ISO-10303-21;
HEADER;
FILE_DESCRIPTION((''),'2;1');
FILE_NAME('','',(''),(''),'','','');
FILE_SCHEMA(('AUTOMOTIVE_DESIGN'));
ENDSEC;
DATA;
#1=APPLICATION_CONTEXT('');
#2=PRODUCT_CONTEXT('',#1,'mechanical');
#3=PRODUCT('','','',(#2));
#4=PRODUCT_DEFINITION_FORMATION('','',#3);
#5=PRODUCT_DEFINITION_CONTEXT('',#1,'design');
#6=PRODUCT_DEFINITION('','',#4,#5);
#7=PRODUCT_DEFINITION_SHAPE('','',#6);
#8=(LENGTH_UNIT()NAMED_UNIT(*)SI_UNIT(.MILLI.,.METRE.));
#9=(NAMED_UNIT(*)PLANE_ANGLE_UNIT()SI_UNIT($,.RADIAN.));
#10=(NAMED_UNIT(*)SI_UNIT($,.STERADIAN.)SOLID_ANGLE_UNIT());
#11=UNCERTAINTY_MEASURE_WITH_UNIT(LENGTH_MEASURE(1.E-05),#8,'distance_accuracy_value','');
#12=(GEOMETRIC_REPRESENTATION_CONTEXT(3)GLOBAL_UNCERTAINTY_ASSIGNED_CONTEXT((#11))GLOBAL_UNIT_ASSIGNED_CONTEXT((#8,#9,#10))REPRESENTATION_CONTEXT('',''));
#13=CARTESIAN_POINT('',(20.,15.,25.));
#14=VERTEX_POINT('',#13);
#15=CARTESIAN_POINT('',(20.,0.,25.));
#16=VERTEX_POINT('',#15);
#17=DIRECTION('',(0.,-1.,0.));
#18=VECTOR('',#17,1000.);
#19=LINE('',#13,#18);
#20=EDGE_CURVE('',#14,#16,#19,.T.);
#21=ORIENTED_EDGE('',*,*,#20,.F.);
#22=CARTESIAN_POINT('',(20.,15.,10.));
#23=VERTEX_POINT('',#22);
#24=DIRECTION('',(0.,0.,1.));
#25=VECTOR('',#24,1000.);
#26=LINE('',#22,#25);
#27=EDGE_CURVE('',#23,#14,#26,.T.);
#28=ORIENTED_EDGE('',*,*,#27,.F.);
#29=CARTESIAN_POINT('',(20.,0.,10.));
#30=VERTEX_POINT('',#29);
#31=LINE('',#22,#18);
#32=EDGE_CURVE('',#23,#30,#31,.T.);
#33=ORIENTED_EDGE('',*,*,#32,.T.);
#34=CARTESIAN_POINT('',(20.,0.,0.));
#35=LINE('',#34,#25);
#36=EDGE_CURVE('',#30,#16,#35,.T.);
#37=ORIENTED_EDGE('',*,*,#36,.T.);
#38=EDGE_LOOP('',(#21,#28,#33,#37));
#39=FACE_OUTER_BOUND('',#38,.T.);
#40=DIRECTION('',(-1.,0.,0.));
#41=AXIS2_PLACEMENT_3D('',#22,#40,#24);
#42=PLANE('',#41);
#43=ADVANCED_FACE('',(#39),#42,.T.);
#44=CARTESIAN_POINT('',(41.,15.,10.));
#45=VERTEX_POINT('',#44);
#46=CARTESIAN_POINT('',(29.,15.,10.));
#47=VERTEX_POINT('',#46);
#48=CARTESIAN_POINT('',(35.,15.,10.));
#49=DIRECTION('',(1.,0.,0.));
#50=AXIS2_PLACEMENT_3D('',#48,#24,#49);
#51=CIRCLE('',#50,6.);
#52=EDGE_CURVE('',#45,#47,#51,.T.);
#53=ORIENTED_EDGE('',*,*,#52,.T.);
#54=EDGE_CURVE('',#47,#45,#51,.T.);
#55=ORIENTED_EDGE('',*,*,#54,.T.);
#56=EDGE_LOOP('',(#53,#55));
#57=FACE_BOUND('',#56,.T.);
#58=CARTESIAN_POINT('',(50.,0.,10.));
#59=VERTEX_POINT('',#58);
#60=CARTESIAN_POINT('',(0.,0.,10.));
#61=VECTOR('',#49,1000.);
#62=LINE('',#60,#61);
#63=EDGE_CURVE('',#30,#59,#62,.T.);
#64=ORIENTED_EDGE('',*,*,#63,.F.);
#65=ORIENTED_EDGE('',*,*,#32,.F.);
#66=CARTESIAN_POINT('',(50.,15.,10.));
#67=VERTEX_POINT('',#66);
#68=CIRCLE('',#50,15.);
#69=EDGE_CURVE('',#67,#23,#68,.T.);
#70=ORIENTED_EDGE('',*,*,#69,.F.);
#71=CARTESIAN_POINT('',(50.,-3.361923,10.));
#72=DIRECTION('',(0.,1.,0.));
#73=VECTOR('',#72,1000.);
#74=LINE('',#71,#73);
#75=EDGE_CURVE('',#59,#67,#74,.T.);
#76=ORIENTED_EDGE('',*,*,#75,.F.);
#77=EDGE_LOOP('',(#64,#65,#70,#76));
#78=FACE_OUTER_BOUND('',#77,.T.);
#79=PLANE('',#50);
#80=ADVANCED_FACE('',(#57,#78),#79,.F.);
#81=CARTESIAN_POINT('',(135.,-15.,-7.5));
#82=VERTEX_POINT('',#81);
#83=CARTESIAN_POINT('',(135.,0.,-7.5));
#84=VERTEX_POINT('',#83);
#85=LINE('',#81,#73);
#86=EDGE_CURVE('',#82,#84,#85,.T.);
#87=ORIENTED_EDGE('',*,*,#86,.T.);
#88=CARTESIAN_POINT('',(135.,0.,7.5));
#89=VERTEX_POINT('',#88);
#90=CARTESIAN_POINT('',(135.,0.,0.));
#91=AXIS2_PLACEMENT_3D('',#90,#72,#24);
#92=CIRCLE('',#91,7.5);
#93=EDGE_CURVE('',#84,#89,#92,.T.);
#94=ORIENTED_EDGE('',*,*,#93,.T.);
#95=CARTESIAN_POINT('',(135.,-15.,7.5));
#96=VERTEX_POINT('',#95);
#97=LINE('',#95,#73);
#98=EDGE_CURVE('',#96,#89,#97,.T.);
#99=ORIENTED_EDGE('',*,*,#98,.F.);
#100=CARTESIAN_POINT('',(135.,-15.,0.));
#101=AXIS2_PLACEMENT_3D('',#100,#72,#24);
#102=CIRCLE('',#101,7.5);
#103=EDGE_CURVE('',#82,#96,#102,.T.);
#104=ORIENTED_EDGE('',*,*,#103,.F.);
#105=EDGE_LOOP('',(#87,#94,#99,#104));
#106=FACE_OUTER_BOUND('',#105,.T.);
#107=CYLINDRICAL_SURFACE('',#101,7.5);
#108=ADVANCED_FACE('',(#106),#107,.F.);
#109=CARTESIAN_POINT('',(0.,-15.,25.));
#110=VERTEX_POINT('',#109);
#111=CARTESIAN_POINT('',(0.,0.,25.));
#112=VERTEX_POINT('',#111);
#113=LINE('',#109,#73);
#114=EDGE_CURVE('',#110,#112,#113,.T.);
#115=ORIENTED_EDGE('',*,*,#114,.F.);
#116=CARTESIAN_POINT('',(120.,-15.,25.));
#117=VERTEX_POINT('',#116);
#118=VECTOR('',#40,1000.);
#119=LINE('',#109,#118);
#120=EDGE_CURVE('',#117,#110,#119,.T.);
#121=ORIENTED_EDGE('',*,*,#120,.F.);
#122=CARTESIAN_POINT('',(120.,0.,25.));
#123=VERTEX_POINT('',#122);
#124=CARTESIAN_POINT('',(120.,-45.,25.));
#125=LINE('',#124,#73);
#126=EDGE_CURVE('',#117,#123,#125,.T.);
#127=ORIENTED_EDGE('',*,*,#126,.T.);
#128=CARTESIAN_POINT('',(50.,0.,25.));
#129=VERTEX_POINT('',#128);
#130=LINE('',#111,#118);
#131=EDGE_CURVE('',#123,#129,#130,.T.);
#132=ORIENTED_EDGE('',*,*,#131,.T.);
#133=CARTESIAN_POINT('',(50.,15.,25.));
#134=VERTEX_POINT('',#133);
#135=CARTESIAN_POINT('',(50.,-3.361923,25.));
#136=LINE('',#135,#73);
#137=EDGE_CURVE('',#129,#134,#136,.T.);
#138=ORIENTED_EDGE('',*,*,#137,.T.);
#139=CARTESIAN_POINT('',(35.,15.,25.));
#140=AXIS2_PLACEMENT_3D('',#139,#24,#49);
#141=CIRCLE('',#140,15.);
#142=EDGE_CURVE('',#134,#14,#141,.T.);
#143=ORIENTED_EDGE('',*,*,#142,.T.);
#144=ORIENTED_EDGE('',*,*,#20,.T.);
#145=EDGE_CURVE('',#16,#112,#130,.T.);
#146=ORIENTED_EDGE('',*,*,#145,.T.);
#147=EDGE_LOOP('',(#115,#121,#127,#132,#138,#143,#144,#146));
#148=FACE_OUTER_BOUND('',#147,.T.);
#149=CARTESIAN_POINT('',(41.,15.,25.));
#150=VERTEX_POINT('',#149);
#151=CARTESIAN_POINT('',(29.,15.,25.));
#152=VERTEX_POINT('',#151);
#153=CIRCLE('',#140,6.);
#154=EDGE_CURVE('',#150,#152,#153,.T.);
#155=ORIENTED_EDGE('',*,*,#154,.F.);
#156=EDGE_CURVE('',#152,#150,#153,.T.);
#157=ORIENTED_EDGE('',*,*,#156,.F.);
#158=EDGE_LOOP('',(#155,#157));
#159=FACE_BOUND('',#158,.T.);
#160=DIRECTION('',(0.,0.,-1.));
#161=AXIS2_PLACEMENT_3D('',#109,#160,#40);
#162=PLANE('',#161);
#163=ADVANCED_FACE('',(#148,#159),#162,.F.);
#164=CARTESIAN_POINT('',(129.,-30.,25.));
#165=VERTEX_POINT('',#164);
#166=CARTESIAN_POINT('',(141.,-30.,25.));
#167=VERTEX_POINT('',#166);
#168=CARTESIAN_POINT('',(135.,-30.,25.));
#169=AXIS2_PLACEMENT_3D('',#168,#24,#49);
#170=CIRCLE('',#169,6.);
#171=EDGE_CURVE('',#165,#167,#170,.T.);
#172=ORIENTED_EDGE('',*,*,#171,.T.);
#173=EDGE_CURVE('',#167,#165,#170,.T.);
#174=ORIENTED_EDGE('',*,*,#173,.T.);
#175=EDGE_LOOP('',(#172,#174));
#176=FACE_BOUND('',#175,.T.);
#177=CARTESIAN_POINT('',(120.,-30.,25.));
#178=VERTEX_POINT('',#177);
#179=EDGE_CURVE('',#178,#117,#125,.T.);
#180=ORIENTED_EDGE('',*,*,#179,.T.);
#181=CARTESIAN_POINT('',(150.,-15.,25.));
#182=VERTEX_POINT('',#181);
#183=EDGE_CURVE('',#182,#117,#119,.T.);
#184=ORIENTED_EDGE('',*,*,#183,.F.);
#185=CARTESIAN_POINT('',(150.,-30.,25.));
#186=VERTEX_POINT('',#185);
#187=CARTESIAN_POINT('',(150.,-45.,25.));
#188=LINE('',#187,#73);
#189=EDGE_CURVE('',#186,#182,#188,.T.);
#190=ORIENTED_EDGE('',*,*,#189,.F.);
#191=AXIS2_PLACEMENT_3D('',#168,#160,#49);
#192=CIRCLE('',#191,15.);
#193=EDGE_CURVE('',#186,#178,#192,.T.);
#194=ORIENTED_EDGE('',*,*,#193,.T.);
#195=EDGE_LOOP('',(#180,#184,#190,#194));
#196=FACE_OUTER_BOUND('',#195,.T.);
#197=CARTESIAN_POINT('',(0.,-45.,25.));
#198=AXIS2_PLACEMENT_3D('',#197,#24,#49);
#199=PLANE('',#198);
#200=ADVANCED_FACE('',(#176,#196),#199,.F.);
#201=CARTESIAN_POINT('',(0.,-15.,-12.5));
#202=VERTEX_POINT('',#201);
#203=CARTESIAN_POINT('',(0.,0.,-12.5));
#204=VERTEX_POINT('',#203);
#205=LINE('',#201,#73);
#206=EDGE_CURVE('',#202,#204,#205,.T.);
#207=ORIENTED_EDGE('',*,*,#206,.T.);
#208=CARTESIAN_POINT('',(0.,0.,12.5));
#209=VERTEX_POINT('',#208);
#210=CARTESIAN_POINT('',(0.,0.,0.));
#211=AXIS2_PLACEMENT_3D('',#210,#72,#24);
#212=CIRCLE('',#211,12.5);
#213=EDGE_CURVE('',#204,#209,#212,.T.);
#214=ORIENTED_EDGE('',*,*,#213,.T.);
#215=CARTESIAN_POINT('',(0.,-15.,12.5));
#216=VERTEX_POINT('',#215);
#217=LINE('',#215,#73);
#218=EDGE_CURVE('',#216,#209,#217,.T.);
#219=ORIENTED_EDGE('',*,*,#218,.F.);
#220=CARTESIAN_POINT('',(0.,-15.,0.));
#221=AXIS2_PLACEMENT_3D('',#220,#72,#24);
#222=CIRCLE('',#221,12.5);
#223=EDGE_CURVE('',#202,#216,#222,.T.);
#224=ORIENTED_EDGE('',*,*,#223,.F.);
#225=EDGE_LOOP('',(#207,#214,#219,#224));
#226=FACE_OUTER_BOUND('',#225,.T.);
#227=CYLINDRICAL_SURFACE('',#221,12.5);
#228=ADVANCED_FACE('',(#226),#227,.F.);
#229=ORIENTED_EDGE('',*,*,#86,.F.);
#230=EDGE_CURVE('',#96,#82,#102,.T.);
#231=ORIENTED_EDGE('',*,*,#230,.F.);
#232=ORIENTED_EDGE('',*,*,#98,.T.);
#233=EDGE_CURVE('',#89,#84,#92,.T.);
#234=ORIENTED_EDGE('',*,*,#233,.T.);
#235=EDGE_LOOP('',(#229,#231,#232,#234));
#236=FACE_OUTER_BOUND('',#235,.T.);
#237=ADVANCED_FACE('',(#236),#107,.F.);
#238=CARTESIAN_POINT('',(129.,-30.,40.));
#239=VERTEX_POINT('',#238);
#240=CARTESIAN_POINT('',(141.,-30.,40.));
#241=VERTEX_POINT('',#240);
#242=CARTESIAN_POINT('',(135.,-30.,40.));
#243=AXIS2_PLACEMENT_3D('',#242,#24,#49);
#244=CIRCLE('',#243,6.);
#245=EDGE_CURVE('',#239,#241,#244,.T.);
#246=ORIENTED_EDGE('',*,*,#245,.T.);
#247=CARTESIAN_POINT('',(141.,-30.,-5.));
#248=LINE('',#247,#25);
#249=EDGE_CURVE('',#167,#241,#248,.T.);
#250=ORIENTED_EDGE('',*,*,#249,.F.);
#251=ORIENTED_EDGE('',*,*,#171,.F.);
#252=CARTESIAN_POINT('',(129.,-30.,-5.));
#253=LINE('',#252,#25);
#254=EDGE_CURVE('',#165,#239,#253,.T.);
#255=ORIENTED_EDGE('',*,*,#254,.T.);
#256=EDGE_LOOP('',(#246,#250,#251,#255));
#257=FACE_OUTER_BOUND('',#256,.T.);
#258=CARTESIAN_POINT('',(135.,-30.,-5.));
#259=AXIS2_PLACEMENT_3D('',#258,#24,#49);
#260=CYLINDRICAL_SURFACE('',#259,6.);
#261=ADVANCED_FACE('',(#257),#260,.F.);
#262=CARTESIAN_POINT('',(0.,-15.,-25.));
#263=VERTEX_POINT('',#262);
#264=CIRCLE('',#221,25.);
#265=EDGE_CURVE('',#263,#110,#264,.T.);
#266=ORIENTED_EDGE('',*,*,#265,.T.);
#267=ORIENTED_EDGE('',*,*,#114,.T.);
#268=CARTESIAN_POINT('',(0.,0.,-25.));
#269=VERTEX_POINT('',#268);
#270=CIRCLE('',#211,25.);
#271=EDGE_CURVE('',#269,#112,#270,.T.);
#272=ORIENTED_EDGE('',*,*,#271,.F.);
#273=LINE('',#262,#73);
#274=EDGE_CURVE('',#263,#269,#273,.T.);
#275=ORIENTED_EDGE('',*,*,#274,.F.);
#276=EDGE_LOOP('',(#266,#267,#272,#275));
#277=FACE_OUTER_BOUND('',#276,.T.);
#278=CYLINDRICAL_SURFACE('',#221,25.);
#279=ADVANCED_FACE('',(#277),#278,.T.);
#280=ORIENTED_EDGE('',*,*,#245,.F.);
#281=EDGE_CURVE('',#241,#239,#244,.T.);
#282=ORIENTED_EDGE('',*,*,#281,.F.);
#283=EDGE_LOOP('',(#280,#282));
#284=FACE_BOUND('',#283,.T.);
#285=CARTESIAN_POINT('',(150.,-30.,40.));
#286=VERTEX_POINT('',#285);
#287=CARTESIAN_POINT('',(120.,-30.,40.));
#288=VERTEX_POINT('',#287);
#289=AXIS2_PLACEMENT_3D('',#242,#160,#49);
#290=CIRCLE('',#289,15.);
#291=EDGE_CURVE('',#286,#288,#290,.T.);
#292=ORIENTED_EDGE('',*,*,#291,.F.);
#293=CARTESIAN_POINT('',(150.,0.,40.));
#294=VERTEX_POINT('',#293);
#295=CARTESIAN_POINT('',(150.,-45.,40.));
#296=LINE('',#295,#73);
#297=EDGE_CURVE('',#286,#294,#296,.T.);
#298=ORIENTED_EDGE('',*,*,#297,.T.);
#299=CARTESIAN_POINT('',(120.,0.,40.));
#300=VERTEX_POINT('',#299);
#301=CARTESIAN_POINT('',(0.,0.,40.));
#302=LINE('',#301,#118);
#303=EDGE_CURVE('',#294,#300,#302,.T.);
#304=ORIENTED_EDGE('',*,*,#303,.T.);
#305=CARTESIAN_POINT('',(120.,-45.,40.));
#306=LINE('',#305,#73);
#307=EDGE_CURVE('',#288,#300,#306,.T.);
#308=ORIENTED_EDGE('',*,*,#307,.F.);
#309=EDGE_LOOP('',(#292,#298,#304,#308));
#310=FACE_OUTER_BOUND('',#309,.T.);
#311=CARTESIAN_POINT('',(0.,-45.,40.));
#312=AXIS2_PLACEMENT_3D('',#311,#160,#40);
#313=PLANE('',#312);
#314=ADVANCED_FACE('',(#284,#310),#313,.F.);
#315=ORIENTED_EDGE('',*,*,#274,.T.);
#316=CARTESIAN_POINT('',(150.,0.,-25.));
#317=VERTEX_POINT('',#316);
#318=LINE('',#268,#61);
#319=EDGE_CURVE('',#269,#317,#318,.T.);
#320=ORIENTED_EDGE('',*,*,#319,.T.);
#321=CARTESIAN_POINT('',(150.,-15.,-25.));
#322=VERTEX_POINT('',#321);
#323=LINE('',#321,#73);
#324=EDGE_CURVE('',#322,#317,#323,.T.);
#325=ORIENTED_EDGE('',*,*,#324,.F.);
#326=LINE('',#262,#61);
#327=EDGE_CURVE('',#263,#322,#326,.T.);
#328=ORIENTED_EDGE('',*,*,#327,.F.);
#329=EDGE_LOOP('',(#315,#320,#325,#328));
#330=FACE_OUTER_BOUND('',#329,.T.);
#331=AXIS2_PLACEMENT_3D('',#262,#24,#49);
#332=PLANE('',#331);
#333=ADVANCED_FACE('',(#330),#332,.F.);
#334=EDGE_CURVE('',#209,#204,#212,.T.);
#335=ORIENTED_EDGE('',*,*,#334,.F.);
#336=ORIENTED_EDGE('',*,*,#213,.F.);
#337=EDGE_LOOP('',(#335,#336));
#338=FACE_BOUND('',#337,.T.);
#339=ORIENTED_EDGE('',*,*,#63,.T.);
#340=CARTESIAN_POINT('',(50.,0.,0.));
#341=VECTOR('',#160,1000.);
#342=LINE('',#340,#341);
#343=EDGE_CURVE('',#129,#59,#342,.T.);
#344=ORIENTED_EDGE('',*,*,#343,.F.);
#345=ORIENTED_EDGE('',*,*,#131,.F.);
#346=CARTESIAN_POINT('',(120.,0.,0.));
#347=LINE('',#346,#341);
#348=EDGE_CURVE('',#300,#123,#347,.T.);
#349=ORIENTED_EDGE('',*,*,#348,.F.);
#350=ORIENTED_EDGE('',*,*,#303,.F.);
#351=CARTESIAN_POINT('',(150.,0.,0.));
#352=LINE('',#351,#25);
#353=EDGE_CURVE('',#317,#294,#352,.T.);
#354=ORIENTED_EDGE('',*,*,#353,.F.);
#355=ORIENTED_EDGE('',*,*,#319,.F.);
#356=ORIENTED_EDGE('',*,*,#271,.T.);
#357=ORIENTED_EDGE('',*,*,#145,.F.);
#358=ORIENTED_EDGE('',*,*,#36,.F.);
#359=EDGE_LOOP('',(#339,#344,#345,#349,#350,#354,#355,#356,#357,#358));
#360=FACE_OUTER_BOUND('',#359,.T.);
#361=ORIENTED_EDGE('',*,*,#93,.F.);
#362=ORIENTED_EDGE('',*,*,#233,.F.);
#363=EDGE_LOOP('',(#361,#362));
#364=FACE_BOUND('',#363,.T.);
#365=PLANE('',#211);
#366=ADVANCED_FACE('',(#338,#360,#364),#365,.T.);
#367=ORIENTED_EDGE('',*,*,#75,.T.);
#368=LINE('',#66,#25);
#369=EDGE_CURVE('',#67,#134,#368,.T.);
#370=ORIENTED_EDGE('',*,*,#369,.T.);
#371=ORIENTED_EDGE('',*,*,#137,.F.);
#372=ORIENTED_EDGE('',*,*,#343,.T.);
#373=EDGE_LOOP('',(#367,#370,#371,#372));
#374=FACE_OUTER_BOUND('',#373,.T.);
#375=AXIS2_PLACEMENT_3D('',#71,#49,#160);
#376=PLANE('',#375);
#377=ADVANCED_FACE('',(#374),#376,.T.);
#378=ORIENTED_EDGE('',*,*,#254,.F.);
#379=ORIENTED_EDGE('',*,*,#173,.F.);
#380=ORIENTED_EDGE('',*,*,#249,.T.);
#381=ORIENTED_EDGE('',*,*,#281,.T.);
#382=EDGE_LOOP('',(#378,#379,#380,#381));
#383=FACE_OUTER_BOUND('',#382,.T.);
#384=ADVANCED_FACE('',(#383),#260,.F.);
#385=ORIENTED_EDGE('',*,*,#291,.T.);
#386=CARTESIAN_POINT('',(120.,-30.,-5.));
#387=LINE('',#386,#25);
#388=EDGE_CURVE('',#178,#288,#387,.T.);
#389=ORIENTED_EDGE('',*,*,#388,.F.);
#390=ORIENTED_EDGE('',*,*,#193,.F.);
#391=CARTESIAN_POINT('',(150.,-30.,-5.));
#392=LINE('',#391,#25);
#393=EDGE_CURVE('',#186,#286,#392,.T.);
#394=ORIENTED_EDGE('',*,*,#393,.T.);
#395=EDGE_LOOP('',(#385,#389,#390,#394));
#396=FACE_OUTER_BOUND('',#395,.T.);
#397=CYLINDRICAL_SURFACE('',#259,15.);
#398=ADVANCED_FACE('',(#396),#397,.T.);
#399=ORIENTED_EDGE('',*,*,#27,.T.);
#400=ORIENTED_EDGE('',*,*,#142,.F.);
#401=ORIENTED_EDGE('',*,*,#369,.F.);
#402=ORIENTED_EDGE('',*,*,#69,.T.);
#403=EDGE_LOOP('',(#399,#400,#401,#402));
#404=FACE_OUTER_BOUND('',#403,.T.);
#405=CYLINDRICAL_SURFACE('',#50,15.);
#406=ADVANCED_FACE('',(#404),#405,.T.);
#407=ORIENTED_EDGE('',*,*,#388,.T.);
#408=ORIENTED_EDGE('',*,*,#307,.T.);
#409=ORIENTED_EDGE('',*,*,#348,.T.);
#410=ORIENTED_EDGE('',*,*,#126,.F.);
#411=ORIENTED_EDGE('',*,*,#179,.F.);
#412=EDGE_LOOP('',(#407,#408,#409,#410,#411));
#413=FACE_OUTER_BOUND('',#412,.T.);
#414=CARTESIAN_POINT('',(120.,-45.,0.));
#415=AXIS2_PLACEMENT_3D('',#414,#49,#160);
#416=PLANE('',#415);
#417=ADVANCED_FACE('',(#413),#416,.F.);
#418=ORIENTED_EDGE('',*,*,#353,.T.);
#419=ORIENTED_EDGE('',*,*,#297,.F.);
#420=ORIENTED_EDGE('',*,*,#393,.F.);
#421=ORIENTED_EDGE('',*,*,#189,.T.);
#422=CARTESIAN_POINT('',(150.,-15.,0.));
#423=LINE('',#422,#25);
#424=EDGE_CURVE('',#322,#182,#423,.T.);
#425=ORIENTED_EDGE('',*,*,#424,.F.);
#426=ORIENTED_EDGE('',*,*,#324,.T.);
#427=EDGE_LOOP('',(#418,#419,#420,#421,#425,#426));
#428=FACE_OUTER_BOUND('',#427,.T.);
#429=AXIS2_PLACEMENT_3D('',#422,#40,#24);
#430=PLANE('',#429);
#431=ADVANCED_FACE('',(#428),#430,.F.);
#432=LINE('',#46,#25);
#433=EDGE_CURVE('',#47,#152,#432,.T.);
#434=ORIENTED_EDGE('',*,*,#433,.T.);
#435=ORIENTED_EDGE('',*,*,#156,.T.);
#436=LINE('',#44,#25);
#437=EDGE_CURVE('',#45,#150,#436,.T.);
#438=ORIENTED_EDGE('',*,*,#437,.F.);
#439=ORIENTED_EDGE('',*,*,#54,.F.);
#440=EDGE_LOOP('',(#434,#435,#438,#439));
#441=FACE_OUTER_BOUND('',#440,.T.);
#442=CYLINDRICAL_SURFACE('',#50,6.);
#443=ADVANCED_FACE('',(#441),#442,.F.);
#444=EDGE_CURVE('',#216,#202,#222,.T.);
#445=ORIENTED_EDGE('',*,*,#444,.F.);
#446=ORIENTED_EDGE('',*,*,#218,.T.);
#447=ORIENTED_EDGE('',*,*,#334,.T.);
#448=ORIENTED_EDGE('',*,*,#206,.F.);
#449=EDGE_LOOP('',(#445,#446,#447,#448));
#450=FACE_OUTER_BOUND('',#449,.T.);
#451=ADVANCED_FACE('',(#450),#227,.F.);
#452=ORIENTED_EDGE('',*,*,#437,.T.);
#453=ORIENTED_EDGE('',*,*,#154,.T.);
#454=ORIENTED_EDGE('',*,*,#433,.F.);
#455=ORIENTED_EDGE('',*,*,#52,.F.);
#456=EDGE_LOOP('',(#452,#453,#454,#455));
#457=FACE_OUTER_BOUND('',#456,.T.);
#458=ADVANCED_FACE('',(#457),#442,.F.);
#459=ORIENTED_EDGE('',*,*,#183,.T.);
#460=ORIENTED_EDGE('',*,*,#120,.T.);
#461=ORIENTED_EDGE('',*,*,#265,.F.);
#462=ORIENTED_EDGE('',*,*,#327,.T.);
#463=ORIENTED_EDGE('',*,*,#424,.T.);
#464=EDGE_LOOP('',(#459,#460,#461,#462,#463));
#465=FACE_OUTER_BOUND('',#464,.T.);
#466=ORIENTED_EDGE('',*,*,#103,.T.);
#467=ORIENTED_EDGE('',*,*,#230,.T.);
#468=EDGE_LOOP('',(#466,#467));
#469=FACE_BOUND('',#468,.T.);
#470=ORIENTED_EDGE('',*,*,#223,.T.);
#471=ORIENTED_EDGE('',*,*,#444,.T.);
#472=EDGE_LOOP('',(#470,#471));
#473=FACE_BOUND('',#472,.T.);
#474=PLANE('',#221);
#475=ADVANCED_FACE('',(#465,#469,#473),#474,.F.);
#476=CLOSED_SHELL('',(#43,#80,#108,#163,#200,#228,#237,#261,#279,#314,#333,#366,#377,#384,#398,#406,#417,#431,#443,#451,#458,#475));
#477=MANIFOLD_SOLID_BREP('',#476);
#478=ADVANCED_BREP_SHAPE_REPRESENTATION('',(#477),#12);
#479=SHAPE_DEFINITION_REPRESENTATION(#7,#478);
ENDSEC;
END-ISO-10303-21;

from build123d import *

# Parameters (mm, degrees)
BASE_PROFILE_SKETCH_R       = 12.5
BASE_PROFILE_SKETCH_R_2     = 7.5
BASE_PLATE_DEPTH            = 15
SKETCH1_3_W                 = 30
SKETCH1_3_H                 = 15
LOWER_LUG_DEPTH             = 45
LOWER_LUG_CUT_SKETCH_R      = 6
LOWER_LUG_PROFILE_CUT_DEPTH = 45
UPRIGHT_LUG_SKETCH_R        = 6
UPRIGHT_LUG_12_HOLE_DEPTH   = 15


with BuildPart() as part:
    # Base Profile Sketch → Base Plate (new body)
    with BuildSketch(Plane(origin=(0, 0, 0), x_dir=(1, 0, 0), z_dir=(0, 1, 0))):
        with BuildLine():
            Line((150, 25), (0, 25))
            ThreePointArc((0, 25), (-25, 0), (0, -25))
            Line((0, -25), (102.111825559, -25))
            Line((102.111825559, -25), (120, -25))
            Line((120, -25), (150, -25))
            Line((150, -25), (150, 25))
        make_face()
        with Locations(Location((0, 0, 0), (0, 0, 270))):
            Circle(BASE_PROFILE_SKETCH_R, mode=Mode.SUBTRACT)
        with Locations(Location((135, 0, 0), (0, 0, 270))):
            Circle(BASE_PROFILE_SKETCH_R_2, mode=Mode.SUBTRACT)
    extrude(amount=-BASE_PLATE_DEPTH)

    # Sketch1_3 → Lower Lug (add)
    with BuildSketch(Plane(origin=(0, 0, 0), x_dir=(1, 0, 0), z_dir=(0, 1, 0))):
        with Locations((135, -32.5)):
            Rectangle(SKETCH1_3_W, SKETCH1_3_H)
    extrude(amount=-LOWER_LUG_DEPTH)

    # Lower Lug Cut Sketch → Lower Lug Profile Cut (cut)
    with BuildSketch(Plane.XY.offset(40)):
        with Locations((135, -30)):
            Circle(LOWER_LUG_CUT_SKETCH_R)
        with BuildLine():
            Line((120, -54.887951231), (153.351111221, -54.269822589))
            Line((153.351111221, -54.269822589), (153.351111221, -31.584501417))
            Line((153.351111221, -31.584501417), (150, -30))
            ThreePointArc((150, -30), (135, -45), (120, -30))
            Line((120, -30), (109.958480534, -30))
            Line((109.958480534, -30), (120, -54.887951231))
        make_face()
    extrude(amount=-LOWER_LUG_PROFILE_CUT_DEPTH, mode=Mode.SUBTRACT)

    # Upright Lug Sketch → Upright Lug _12 Hole (add)
    with BuildSketch(Plane.XY.offset(25)):
        with BuildLine():
            Line((20, 15), (20, -3.361922894))
            Line((20, -3.361922894), (50, -3.361922894))
            Line((50, -3.361922894), (50, 15))
            ThreePointArc((50, 15), (35, 30), (20, 15))
        make_face()
        with Locations((35, 15)):
            Circle(UPRIGHT_LUG_SKETCH_R, mode=Mode.SUBTRACT)
    extrude(amount=-UPRIGHT_LUG_12_HOLE_DEPTH)


solid = part.part
